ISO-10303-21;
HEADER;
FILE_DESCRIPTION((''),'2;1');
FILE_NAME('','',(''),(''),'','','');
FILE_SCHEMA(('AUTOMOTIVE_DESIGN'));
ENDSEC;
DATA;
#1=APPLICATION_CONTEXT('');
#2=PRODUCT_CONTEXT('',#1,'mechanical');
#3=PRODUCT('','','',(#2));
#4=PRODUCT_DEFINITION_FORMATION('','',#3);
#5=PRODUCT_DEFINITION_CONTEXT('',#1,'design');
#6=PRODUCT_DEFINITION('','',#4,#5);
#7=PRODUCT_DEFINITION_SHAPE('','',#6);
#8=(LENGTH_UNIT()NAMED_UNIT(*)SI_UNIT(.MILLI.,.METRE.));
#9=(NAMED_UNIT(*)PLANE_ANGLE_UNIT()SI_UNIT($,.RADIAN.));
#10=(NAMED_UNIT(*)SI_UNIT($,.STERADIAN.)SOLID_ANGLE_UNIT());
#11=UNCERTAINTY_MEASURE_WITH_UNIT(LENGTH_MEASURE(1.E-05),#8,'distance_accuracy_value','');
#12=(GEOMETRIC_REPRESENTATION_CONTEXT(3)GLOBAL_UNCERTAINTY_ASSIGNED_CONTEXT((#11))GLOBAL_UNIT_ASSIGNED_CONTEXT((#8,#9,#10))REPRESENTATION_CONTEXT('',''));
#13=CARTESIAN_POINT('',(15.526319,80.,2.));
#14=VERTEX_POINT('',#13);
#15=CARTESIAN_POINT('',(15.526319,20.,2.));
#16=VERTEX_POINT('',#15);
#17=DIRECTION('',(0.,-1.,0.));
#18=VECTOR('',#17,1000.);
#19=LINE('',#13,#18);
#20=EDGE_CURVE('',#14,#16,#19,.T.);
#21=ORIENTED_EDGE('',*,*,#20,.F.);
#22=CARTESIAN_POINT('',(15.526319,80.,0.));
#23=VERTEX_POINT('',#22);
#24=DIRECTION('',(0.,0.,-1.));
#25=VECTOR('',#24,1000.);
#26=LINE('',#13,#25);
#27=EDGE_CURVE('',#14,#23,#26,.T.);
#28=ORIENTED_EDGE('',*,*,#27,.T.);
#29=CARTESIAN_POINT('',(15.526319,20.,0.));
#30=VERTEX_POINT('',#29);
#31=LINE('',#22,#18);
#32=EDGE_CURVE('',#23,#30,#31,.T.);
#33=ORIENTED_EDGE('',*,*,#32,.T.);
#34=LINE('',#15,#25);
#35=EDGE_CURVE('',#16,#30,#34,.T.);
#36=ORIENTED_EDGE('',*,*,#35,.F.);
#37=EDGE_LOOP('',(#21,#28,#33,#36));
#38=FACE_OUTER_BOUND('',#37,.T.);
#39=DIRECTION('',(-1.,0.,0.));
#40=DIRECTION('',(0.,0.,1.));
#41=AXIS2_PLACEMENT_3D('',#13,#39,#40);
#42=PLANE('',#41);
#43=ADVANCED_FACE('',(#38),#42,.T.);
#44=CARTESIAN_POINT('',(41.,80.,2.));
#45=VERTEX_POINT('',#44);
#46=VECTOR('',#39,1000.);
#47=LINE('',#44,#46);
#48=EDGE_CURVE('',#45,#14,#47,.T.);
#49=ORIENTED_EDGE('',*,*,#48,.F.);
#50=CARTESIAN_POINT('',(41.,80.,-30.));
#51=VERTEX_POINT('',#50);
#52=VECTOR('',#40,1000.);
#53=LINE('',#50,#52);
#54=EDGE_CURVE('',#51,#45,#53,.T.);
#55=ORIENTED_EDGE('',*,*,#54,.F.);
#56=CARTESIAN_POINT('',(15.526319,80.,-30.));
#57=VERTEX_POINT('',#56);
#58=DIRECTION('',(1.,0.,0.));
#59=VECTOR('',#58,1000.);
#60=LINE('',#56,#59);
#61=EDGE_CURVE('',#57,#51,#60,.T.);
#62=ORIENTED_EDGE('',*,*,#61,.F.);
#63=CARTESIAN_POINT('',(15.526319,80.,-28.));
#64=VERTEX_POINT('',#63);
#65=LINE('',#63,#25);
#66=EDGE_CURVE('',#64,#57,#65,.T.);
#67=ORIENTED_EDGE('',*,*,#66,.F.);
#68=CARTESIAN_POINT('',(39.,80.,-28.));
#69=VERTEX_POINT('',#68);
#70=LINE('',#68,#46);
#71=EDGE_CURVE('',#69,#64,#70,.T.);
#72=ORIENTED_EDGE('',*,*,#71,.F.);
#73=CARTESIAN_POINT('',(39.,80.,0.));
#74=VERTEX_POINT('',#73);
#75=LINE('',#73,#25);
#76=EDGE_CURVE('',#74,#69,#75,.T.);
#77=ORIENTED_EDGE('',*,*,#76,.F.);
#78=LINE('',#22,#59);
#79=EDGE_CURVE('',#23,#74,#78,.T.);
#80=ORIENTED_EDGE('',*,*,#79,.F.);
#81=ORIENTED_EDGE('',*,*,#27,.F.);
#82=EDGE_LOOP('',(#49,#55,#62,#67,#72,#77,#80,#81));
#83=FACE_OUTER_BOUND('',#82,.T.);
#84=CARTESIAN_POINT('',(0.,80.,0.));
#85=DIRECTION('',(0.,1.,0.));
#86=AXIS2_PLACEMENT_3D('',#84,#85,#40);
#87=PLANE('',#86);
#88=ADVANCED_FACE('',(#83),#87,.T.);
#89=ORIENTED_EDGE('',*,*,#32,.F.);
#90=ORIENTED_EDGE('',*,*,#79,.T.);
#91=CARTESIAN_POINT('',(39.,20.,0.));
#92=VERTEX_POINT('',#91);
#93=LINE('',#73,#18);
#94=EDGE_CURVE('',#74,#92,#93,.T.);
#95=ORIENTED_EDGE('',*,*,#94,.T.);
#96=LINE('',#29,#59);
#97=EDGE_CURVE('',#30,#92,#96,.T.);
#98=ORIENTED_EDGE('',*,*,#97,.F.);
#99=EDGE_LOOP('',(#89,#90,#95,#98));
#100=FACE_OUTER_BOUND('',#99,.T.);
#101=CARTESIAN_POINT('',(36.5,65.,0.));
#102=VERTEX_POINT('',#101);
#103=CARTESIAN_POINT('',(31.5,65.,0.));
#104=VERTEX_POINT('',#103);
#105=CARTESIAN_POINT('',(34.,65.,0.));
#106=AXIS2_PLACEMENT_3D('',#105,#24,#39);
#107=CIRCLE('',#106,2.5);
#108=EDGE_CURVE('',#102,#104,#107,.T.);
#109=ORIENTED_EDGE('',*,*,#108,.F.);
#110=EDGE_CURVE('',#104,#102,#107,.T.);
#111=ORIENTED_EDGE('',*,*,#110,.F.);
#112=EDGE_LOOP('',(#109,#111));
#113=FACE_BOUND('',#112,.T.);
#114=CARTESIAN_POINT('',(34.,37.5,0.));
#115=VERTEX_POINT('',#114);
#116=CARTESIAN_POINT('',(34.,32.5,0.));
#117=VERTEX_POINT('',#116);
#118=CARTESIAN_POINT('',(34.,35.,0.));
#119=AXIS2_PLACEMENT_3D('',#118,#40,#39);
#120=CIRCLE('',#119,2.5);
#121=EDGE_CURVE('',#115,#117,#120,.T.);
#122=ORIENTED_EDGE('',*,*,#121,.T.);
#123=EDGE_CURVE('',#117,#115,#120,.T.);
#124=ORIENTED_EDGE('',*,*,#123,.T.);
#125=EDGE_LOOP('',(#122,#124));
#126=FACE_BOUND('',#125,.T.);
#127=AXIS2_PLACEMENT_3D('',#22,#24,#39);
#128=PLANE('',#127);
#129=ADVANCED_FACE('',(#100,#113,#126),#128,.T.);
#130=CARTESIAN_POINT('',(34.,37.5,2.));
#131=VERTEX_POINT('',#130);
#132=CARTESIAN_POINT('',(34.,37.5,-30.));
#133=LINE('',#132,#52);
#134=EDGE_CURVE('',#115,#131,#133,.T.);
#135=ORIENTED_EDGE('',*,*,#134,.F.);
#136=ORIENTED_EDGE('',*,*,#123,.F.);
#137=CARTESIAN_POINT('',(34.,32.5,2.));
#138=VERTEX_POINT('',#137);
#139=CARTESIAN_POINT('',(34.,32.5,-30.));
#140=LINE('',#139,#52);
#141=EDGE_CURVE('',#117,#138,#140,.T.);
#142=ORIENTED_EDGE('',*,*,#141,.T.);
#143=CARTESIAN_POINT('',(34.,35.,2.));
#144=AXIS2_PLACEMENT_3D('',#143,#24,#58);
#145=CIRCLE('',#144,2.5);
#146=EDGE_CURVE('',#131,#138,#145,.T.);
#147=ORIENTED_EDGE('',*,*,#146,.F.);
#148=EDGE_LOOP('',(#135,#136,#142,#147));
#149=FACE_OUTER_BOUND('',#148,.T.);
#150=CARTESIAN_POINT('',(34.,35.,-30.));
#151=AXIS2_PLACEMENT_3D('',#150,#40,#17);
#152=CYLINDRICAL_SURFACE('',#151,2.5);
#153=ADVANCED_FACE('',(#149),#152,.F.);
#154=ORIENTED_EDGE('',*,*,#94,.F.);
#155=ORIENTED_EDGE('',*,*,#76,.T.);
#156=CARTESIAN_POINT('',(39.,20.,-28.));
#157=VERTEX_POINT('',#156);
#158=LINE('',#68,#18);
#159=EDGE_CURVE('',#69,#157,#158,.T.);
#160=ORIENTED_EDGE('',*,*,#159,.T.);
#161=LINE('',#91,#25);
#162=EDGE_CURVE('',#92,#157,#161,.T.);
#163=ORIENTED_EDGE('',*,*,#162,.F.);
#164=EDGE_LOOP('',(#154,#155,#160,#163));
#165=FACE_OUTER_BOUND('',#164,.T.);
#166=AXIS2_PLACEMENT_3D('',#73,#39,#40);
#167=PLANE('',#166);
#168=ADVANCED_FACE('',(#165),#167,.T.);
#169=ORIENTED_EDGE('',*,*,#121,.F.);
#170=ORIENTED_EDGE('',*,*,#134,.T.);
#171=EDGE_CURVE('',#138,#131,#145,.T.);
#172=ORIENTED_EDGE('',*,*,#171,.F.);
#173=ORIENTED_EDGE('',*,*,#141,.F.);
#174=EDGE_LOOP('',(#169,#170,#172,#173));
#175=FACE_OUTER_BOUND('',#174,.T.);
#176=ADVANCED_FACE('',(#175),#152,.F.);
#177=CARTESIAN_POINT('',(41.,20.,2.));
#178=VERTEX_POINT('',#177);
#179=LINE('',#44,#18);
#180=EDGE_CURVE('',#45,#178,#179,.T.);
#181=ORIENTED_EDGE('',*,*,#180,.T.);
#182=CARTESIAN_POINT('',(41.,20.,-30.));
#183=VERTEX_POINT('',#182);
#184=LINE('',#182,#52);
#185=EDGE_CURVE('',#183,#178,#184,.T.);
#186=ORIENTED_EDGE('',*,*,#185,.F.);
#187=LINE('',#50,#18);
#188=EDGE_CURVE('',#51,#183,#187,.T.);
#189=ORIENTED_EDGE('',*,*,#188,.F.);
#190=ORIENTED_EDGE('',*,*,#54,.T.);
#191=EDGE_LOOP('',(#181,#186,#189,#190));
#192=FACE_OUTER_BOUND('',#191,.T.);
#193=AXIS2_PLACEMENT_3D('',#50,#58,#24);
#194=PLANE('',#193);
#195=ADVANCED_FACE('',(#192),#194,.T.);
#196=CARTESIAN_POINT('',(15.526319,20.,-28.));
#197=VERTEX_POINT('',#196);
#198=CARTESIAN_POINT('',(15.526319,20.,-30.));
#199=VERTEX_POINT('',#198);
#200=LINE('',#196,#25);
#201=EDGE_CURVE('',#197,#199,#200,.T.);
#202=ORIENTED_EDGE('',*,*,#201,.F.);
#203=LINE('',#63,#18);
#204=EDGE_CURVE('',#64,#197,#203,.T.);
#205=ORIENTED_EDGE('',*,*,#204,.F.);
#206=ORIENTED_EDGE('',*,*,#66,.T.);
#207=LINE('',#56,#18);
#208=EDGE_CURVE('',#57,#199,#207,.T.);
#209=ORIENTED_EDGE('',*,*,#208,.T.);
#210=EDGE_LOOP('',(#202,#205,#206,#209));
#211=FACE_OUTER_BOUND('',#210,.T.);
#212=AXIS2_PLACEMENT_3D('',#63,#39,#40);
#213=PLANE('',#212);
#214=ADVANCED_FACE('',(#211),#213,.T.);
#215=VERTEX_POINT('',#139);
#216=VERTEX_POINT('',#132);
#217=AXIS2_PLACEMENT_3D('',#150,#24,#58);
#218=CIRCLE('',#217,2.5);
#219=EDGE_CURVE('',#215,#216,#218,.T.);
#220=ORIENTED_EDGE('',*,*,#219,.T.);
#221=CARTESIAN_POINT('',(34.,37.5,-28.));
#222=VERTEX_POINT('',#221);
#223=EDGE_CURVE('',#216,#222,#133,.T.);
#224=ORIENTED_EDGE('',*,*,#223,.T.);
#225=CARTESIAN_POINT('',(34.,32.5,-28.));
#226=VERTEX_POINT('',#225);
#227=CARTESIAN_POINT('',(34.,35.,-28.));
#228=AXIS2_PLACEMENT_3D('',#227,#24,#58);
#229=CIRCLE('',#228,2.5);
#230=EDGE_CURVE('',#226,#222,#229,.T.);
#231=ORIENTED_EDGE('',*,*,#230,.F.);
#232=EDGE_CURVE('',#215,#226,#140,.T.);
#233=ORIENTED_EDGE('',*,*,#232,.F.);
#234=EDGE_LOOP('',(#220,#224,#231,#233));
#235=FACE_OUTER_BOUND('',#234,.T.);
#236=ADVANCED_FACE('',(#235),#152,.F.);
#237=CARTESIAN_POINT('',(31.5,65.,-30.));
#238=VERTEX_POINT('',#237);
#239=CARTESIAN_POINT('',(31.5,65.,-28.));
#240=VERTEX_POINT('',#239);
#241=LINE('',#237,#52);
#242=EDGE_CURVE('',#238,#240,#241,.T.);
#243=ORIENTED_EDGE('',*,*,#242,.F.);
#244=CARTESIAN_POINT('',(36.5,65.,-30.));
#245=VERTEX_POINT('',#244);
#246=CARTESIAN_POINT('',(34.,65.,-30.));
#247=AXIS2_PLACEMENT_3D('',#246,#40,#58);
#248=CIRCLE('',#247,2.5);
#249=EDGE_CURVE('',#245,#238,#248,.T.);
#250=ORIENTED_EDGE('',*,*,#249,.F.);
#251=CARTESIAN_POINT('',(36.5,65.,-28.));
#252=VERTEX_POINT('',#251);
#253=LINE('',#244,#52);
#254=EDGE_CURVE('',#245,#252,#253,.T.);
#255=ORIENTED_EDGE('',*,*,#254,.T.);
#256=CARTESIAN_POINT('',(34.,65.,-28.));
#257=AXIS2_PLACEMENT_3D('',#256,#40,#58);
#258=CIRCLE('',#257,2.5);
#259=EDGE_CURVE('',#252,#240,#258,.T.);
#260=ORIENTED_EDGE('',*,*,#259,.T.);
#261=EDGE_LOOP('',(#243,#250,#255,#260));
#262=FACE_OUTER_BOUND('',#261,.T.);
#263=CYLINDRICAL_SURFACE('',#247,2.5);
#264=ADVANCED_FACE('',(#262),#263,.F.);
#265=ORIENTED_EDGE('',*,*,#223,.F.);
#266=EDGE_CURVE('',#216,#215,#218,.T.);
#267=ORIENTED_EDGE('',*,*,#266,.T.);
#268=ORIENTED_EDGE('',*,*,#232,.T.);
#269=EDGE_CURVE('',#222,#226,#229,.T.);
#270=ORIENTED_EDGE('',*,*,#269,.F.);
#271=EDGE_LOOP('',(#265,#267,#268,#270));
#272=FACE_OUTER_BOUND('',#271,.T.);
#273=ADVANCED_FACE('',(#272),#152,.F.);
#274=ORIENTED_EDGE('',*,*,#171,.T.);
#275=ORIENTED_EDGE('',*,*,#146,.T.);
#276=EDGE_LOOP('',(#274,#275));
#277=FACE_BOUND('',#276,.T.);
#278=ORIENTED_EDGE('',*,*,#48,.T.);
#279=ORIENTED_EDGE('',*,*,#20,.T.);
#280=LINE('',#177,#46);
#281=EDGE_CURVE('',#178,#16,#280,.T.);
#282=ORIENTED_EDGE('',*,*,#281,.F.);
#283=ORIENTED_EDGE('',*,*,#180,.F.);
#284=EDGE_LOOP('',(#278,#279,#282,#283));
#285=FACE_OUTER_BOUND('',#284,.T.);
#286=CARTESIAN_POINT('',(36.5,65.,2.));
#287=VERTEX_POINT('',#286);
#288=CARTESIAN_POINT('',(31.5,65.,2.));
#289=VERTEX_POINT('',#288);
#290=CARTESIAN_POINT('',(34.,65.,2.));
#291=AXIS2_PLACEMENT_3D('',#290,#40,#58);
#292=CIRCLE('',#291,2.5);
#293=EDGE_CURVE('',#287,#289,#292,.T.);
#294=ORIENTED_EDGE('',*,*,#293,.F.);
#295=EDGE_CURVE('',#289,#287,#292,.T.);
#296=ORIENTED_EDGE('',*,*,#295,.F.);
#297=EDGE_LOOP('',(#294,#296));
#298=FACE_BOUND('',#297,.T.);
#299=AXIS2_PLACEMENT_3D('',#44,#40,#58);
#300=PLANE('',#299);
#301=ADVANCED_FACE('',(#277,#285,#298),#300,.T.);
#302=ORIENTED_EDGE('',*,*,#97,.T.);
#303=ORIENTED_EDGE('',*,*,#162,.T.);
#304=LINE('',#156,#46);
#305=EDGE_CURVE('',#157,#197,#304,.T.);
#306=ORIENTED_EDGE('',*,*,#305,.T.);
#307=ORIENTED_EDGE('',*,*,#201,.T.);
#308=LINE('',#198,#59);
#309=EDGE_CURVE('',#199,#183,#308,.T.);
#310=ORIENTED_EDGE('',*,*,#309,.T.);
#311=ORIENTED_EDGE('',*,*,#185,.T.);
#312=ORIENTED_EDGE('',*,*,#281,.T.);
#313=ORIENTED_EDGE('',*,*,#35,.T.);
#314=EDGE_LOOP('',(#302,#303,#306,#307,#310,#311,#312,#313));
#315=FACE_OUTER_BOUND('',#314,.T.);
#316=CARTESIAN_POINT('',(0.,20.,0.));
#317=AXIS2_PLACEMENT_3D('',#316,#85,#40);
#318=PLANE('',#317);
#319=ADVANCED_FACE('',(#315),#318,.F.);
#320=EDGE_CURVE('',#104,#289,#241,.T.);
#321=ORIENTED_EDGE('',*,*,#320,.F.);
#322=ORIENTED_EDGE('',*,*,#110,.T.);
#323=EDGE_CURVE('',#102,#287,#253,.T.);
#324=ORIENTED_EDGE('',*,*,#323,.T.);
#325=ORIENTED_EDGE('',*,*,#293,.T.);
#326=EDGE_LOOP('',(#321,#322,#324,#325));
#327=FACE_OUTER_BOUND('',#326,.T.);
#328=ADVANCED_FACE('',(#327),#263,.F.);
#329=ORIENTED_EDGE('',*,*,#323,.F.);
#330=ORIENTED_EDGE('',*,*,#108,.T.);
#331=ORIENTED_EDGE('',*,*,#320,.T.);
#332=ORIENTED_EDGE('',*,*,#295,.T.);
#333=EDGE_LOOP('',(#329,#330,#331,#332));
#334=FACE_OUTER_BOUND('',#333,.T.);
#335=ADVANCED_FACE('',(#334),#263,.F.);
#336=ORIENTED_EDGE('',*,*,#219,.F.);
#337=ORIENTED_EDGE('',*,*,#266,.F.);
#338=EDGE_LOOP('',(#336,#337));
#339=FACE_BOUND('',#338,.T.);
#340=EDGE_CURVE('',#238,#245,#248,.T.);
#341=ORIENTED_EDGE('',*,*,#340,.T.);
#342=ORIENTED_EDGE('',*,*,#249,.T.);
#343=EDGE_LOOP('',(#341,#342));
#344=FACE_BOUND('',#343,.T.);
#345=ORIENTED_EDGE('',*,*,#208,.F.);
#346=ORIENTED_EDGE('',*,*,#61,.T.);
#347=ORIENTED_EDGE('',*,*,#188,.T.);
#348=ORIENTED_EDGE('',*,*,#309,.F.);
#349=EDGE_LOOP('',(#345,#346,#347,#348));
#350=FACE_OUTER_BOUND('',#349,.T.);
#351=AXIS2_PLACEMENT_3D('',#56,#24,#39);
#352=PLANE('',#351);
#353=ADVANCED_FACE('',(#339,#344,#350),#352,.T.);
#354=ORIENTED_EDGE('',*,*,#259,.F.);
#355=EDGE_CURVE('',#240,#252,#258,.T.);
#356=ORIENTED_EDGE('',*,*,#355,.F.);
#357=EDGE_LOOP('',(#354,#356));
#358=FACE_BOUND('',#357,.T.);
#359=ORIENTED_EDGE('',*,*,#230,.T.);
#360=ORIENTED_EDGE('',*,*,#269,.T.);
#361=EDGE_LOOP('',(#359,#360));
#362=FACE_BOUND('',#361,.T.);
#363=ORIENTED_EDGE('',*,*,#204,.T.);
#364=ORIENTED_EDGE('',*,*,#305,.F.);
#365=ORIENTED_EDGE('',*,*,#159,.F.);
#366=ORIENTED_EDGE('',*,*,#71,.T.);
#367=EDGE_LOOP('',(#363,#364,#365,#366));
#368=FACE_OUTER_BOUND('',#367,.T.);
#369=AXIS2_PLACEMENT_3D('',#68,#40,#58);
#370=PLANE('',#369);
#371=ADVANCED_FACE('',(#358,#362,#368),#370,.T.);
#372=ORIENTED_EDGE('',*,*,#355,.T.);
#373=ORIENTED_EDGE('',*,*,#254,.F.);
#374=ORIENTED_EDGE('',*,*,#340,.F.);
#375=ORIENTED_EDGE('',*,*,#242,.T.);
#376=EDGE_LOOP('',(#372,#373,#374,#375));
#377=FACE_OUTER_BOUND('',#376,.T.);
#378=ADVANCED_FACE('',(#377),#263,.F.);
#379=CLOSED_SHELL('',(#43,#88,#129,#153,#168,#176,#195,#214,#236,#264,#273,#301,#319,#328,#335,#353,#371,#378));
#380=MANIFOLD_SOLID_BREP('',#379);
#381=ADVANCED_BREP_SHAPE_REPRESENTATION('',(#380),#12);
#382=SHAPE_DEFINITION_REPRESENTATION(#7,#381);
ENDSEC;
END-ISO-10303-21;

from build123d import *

# Parameters (mm, degrees)
BOSS_EXTRUDE1_DEPTH      = 30
BOSS_EXTRUDE1_DEPTH_BACK = 30
SKETCH3_R                = 2.5
CUT_EXTRUDE1_DEPTH       = 96.420123664


with BuildPart() as part:
    # Sketch2 → Boss-Extrude1 (new, two sides: drawn at the far end of the back side and taken through both)
    with BuildSketch(Plane(origin=(0, 50, 0), x_dir=(-1, 0, 0), z_dir=(0, -1, 0)).offset(-BOSS_EXTRUDE1_DEPTH_BACK)):
        Polygon((-39, 28), (-15.526318688, 28), (-15.526318688, 30), (-41, 30), (-41, -2), (-15.526318688, -2), (-15.526318688, 0), (-39, 0), align=None)
    extrude(amount=BOSS_EXTRUDE1_DEPTH + BOSS_EXTRUDE1_DEPTH_BACK)

    # Sketch3 → Cut-Extrude1 (cut, symmetric)
    with BuildSketch(Plane.XY.offset(2)):
        with Locations((34, 65)):
            Circle(SKETCH3_R)
    cut_extrude1 = extrude(amount=CUT_EXTRUDE1_DEPTH, both=True, mode=Mode.SUBTRACT)

    # Mirror1: Cut-Extrude1 across plane
    add(cut_extrude1.mirror(Plane(origin=(0, 50, 0), x_dir=(0, 0, 1), z_dir=(0, -1, 0))), mode=Mode.SUBTRACT)


solid = part.part
